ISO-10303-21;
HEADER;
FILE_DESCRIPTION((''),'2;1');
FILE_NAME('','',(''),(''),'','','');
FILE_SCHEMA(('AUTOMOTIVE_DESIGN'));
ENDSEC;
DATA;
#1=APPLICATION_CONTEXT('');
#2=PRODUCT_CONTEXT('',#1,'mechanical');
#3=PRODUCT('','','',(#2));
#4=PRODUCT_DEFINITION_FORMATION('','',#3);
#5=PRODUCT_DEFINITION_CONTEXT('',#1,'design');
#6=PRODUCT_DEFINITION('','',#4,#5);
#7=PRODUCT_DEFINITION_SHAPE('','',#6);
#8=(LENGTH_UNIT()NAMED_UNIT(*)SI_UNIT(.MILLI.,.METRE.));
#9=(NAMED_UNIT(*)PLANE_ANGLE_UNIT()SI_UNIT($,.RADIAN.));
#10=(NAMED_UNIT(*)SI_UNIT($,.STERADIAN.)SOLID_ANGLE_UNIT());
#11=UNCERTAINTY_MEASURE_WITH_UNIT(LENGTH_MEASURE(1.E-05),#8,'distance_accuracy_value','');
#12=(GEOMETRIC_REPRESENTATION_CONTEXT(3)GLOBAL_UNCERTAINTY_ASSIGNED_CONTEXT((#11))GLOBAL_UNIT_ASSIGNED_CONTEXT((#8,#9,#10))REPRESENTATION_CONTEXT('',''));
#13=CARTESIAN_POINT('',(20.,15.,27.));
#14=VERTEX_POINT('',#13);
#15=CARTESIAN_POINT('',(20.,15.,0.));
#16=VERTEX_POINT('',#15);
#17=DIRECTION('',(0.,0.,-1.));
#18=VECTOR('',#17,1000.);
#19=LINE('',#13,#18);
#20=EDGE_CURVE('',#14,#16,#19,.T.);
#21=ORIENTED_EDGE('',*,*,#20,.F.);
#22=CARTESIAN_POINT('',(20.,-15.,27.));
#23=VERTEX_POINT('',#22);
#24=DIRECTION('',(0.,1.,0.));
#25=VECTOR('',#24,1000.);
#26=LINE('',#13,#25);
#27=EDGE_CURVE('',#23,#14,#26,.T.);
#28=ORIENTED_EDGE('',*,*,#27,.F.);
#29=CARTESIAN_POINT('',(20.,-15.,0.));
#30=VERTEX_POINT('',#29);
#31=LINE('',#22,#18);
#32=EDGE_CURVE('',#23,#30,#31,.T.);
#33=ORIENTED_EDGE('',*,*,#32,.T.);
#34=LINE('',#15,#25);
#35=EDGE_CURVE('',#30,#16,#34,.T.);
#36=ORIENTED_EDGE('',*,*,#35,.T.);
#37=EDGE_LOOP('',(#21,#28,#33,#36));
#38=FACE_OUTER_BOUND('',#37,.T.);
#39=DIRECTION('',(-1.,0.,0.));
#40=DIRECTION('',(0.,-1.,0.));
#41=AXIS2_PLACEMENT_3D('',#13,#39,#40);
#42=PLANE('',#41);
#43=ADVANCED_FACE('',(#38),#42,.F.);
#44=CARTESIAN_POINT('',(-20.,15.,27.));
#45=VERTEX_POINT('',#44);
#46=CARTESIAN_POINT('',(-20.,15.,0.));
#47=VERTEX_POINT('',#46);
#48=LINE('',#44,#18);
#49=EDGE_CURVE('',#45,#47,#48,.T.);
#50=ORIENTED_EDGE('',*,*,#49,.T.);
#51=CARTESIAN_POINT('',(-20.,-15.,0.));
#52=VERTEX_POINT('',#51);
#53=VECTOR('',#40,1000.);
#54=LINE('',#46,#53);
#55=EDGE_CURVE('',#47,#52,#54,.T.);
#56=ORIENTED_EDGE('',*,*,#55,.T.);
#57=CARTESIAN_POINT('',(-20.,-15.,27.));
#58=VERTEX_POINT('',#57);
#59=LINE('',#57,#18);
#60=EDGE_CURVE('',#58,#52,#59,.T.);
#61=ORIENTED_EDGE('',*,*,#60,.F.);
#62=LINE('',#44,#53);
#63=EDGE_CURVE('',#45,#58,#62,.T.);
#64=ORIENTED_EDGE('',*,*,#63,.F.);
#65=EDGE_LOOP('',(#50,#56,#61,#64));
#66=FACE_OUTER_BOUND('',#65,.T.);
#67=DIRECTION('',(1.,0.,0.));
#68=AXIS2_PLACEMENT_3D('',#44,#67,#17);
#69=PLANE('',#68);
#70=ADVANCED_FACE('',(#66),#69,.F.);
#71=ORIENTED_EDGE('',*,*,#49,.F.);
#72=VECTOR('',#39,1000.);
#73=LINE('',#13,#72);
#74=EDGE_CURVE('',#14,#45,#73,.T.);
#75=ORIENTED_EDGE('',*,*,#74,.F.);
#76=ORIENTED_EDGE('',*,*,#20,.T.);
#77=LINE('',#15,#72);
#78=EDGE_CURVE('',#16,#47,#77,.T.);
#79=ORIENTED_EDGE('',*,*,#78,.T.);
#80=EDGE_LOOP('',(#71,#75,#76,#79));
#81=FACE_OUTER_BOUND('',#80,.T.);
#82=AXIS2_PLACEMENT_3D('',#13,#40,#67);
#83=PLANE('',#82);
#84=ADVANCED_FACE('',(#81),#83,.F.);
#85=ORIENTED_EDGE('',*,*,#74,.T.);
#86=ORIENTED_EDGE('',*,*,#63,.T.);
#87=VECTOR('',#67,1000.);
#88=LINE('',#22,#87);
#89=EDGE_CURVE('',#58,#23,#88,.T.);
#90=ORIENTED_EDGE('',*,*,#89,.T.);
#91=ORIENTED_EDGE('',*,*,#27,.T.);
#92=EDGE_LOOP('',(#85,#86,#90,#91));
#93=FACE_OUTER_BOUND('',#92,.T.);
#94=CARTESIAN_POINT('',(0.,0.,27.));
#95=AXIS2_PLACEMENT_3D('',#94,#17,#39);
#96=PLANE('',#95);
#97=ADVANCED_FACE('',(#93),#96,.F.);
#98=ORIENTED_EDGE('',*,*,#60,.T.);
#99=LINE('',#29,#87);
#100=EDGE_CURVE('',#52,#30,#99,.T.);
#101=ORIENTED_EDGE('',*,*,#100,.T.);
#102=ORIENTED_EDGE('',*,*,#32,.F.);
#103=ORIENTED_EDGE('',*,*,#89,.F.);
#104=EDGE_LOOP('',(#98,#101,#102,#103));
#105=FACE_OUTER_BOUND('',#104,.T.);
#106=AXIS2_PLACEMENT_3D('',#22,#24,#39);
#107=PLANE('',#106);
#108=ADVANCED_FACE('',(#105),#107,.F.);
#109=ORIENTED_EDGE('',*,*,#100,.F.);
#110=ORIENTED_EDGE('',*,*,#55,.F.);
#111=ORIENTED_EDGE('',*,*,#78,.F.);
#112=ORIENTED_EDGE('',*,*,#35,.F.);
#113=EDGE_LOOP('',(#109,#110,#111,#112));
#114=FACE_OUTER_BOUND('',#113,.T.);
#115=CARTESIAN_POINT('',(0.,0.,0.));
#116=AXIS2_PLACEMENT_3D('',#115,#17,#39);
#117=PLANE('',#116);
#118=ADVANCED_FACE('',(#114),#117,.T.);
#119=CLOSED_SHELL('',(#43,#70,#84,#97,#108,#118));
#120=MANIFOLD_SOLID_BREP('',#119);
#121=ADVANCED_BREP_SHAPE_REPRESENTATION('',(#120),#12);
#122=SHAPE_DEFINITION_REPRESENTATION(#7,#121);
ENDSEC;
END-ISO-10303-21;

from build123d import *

# Parameters (mm, degrees)
SKETCH1_W           = 40
SKETCH1_H           = 30
BOSS_EXTRUDE1_DEPTH = 27


with BuildPart() as part:
    # Sketch1 → Boss-Extrude1 (new body)
    with BuildSketch(Plane.XY):
        Rectangle(SKETCH1_W, SKETCH1_H)
    extrude(amount=BOSS_EXTRUDE1_DEPTH)


solid = part.part
